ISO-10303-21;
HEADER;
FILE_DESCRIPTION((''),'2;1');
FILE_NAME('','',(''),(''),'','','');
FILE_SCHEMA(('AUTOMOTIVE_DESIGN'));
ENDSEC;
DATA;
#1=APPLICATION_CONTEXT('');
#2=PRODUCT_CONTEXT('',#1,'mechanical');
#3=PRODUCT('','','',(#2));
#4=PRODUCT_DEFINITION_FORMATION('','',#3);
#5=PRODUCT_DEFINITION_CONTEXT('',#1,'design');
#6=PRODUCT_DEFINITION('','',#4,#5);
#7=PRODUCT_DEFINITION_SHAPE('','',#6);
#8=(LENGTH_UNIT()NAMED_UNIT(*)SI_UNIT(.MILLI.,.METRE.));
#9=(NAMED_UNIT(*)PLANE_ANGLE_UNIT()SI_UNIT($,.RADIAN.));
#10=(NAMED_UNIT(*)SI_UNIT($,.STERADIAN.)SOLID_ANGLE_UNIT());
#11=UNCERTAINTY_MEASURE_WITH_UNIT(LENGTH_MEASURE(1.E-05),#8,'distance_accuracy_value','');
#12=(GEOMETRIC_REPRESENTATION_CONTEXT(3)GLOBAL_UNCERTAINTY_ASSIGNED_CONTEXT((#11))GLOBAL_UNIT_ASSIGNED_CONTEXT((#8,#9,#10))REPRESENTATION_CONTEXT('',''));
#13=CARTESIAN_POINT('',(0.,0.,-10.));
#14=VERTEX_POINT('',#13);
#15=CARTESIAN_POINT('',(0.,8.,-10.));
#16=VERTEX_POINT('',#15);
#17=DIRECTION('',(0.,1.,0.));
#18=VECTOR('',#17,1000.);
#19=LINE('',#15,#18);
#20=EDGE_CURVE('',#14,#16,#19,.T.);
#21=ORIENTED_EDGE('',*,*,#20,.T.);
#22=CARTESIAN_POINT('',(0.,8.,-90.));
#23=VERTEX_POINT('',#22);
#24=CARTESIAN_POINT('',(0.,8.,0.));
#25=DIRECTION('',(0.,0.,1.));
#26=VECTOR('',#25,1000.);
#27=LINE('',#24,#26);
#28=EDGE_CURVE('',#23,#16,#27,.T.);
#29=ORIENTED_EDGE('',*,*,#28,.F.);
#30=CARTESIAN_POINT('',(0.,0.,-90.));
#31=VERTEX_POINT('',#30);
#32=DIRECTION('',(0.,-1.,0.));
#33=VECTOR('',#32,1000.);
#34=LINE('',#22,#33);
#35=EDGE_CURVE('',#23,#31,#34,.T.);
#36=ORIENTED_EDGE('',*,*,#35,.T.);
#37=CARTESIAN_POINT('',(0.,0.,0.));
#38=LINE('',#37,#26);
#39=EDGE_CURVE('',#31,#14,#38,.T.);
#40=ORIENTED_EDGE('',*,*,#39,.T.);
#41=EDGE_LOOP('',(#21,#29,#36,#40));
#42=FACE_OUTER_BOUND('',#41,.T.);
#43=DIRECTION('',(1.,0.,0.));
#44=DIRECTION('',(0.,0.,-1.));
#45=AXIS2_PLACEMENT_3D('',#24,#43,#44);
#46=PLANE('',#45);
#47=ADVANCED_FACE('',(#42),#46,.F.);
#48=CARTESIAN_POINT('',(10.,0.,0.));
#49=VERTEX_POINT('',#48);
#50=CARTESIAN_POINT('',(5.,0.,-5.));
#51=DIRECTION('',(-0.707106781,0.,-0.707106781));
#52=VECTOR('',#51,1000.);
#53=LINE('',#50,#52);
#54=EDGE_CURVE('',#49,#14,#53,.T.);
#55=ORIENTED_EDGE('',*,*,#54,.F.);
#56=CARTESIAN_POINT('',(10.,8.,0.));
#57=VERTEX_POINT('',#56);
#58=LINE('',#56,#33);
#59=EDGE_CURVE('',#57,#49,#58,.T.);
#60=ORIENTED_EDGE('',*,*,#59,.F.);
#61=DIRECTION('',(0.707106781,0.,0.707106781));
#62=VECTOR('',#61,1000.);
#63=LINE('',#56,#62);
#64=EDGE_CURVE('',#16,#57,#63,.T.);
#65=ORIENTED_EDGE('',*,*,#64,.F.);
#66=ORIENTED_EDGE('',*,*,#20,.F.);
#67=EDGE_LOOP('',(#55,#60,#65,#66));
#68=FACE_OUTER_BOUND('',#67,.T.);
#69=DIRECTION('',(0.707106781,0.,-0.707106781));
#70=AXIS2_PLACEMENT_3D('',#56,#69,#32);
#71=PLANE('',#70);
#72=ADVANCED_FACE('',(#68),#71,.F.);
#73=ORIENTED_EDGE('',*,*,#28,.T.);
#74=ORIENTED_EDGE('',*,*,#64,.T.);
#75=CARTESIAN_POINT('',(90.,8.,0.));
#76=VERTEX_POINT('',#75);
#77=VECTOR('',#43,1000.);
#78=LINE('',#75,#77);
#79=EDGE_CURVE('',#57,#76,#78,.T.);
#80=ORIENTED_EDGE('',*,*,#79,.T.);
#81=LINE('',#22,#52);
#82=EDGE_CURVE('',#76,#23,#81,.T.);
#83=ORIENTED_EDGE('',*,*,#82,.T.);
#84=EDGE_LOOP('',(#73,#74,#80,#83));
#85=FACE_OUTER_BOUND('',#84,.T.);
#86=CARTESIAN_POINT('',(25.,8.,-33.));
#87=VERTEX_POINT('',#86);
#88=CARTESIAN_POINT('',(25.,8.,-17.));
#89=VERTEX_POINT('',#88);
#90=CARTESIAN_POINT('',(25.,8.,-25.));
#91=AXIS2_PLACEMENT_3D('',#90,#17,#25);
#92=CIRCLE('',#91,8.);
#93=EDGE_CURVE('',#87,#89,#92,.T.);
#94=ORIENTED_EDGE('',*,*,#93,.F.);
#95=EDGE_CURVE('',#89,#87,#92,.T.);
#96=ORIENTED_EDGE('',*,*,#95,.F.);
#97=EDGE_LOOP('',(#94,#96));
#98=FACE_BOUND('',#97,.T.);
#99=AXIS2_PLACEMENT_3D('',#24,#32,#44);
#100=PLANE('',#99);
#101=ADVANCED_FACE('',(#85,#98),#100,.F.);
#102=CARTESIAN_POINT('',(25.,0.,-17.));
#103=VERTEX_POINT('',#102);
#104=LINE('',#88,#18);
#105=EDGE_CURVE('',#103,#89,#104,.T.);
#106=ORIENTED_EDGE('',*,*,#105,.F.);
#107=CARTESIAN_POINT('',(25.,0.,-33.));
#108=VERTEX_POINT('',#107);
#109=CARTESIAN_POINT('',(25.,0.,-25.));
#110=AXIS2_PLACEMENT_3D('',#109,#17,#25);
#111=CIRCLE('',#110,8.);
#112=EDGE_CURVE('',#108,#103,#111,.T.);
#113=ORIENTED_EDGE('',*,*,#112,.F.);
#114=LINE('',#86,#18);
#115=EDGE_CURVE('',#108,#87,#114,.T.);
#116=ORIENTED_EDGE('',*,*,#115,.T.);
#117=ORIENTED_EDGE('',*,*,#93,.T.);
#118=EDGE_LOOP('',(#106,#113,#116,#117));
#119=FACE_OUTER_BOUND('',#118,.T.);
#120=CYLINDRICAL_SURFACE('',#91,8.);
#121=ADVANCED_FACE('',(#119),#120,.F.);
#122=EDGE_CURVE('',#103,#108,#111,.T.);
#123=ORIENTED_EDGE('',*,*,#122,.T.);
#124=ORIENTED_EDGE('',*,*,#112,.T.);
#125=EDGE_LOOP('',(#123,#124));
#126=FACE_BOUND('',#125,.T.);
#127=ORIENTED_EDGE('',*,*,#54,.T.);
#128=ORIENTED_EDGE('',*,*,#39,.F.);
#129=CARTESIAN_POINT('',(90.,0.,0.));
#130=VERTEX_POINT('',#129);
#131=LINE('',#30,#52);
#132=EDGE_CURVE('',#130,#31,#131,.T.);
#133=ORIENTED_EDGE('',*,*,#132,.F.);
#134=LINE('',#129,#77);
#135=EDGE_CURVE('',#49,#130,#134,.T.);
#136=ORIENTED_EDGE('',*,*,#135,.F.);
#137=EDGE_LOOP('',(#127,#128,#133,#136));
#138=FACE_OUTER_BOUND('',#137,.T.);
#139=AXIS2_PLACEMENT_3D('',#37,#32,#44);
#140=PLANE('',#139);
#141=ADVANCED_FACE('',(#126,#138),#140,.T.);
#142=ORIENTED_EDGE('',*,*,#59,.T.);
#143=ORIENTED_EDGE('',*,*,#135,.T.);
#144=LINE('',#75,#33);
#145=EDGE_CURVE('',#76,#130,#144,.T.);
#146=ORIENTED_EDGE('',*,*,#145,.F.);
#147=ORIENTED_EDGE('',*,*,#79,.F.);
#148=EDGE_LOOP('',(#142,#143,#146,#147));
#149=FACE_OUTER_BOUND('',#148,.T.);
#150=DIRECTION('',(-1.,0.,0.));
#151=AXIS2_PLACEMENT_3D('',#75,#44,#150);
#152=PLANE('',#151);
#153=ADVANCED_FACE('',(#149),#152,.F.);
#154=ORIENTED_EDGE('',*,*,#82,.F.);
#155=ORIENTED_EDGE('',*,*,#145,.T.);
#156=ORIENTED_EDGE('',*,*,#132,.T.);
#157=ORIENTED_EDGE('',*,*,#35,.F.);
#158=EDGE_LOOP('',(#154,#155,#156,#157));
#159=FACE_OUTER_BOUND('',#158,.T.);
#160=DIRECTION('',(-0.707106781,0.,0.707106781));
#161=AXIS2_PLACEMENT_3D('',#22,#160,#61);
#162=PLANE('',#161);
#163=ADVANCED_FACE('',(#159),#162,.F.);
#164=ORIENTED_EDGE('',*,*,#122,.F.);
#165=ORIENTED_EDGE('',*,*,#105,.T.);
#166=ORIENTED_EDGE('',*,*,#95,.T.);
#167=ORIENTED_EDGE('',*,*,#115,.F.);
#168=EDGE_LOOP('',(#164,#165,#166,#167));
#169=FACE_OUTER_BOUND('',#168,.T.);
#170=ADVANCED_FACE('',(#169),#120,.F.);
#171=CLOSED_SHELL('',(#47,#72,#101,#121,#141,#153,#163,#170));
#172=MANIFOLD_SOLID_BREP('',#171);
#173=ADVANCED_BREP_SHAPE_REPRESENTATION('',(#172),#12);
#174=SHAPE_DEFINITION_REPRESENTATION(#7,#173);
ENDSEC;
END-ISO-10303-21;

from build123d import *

# Parameters (mm, degrees)
EXTRUDE_1_DEPTH         = 8
CHAMFER_1_SIZE          = 10
HOLE_WIZARD_16_0_16_1_D = 16


with BuildPart() as part:
    # 草图1 → 凸台-拉伸1 (new body)
    with BuildSketch(Plane(origin=(0, 0, 0), x_dir=(1, 0, 0), z_dir=(0, 1, 0))):
        Polygon((0, 0), (0, 90), (90, 0), align=None)
    extrude(amount=EXTRUDE_1_DEPTH)

    # 倒角1
    chamfer_1_edges = [part.edges().sort_by_distance(p)[0] for p in [
        (0, 4, 0),
    ]]
    chamfer(chamfer_1_edges, length=CHAMFER_1_SIZE)

    # Ø16.0 (16) 直径孔1 (through all)
    with Locations(Plane(origin=(0, 8, 0), x_dir=(1, 0, 0), z_dir=(0, 1, 0))):
        with Locations((25, 25)):
            Hole(HOLE_WIZARD_16_0_16_1_D / 2)


solid = part.part
